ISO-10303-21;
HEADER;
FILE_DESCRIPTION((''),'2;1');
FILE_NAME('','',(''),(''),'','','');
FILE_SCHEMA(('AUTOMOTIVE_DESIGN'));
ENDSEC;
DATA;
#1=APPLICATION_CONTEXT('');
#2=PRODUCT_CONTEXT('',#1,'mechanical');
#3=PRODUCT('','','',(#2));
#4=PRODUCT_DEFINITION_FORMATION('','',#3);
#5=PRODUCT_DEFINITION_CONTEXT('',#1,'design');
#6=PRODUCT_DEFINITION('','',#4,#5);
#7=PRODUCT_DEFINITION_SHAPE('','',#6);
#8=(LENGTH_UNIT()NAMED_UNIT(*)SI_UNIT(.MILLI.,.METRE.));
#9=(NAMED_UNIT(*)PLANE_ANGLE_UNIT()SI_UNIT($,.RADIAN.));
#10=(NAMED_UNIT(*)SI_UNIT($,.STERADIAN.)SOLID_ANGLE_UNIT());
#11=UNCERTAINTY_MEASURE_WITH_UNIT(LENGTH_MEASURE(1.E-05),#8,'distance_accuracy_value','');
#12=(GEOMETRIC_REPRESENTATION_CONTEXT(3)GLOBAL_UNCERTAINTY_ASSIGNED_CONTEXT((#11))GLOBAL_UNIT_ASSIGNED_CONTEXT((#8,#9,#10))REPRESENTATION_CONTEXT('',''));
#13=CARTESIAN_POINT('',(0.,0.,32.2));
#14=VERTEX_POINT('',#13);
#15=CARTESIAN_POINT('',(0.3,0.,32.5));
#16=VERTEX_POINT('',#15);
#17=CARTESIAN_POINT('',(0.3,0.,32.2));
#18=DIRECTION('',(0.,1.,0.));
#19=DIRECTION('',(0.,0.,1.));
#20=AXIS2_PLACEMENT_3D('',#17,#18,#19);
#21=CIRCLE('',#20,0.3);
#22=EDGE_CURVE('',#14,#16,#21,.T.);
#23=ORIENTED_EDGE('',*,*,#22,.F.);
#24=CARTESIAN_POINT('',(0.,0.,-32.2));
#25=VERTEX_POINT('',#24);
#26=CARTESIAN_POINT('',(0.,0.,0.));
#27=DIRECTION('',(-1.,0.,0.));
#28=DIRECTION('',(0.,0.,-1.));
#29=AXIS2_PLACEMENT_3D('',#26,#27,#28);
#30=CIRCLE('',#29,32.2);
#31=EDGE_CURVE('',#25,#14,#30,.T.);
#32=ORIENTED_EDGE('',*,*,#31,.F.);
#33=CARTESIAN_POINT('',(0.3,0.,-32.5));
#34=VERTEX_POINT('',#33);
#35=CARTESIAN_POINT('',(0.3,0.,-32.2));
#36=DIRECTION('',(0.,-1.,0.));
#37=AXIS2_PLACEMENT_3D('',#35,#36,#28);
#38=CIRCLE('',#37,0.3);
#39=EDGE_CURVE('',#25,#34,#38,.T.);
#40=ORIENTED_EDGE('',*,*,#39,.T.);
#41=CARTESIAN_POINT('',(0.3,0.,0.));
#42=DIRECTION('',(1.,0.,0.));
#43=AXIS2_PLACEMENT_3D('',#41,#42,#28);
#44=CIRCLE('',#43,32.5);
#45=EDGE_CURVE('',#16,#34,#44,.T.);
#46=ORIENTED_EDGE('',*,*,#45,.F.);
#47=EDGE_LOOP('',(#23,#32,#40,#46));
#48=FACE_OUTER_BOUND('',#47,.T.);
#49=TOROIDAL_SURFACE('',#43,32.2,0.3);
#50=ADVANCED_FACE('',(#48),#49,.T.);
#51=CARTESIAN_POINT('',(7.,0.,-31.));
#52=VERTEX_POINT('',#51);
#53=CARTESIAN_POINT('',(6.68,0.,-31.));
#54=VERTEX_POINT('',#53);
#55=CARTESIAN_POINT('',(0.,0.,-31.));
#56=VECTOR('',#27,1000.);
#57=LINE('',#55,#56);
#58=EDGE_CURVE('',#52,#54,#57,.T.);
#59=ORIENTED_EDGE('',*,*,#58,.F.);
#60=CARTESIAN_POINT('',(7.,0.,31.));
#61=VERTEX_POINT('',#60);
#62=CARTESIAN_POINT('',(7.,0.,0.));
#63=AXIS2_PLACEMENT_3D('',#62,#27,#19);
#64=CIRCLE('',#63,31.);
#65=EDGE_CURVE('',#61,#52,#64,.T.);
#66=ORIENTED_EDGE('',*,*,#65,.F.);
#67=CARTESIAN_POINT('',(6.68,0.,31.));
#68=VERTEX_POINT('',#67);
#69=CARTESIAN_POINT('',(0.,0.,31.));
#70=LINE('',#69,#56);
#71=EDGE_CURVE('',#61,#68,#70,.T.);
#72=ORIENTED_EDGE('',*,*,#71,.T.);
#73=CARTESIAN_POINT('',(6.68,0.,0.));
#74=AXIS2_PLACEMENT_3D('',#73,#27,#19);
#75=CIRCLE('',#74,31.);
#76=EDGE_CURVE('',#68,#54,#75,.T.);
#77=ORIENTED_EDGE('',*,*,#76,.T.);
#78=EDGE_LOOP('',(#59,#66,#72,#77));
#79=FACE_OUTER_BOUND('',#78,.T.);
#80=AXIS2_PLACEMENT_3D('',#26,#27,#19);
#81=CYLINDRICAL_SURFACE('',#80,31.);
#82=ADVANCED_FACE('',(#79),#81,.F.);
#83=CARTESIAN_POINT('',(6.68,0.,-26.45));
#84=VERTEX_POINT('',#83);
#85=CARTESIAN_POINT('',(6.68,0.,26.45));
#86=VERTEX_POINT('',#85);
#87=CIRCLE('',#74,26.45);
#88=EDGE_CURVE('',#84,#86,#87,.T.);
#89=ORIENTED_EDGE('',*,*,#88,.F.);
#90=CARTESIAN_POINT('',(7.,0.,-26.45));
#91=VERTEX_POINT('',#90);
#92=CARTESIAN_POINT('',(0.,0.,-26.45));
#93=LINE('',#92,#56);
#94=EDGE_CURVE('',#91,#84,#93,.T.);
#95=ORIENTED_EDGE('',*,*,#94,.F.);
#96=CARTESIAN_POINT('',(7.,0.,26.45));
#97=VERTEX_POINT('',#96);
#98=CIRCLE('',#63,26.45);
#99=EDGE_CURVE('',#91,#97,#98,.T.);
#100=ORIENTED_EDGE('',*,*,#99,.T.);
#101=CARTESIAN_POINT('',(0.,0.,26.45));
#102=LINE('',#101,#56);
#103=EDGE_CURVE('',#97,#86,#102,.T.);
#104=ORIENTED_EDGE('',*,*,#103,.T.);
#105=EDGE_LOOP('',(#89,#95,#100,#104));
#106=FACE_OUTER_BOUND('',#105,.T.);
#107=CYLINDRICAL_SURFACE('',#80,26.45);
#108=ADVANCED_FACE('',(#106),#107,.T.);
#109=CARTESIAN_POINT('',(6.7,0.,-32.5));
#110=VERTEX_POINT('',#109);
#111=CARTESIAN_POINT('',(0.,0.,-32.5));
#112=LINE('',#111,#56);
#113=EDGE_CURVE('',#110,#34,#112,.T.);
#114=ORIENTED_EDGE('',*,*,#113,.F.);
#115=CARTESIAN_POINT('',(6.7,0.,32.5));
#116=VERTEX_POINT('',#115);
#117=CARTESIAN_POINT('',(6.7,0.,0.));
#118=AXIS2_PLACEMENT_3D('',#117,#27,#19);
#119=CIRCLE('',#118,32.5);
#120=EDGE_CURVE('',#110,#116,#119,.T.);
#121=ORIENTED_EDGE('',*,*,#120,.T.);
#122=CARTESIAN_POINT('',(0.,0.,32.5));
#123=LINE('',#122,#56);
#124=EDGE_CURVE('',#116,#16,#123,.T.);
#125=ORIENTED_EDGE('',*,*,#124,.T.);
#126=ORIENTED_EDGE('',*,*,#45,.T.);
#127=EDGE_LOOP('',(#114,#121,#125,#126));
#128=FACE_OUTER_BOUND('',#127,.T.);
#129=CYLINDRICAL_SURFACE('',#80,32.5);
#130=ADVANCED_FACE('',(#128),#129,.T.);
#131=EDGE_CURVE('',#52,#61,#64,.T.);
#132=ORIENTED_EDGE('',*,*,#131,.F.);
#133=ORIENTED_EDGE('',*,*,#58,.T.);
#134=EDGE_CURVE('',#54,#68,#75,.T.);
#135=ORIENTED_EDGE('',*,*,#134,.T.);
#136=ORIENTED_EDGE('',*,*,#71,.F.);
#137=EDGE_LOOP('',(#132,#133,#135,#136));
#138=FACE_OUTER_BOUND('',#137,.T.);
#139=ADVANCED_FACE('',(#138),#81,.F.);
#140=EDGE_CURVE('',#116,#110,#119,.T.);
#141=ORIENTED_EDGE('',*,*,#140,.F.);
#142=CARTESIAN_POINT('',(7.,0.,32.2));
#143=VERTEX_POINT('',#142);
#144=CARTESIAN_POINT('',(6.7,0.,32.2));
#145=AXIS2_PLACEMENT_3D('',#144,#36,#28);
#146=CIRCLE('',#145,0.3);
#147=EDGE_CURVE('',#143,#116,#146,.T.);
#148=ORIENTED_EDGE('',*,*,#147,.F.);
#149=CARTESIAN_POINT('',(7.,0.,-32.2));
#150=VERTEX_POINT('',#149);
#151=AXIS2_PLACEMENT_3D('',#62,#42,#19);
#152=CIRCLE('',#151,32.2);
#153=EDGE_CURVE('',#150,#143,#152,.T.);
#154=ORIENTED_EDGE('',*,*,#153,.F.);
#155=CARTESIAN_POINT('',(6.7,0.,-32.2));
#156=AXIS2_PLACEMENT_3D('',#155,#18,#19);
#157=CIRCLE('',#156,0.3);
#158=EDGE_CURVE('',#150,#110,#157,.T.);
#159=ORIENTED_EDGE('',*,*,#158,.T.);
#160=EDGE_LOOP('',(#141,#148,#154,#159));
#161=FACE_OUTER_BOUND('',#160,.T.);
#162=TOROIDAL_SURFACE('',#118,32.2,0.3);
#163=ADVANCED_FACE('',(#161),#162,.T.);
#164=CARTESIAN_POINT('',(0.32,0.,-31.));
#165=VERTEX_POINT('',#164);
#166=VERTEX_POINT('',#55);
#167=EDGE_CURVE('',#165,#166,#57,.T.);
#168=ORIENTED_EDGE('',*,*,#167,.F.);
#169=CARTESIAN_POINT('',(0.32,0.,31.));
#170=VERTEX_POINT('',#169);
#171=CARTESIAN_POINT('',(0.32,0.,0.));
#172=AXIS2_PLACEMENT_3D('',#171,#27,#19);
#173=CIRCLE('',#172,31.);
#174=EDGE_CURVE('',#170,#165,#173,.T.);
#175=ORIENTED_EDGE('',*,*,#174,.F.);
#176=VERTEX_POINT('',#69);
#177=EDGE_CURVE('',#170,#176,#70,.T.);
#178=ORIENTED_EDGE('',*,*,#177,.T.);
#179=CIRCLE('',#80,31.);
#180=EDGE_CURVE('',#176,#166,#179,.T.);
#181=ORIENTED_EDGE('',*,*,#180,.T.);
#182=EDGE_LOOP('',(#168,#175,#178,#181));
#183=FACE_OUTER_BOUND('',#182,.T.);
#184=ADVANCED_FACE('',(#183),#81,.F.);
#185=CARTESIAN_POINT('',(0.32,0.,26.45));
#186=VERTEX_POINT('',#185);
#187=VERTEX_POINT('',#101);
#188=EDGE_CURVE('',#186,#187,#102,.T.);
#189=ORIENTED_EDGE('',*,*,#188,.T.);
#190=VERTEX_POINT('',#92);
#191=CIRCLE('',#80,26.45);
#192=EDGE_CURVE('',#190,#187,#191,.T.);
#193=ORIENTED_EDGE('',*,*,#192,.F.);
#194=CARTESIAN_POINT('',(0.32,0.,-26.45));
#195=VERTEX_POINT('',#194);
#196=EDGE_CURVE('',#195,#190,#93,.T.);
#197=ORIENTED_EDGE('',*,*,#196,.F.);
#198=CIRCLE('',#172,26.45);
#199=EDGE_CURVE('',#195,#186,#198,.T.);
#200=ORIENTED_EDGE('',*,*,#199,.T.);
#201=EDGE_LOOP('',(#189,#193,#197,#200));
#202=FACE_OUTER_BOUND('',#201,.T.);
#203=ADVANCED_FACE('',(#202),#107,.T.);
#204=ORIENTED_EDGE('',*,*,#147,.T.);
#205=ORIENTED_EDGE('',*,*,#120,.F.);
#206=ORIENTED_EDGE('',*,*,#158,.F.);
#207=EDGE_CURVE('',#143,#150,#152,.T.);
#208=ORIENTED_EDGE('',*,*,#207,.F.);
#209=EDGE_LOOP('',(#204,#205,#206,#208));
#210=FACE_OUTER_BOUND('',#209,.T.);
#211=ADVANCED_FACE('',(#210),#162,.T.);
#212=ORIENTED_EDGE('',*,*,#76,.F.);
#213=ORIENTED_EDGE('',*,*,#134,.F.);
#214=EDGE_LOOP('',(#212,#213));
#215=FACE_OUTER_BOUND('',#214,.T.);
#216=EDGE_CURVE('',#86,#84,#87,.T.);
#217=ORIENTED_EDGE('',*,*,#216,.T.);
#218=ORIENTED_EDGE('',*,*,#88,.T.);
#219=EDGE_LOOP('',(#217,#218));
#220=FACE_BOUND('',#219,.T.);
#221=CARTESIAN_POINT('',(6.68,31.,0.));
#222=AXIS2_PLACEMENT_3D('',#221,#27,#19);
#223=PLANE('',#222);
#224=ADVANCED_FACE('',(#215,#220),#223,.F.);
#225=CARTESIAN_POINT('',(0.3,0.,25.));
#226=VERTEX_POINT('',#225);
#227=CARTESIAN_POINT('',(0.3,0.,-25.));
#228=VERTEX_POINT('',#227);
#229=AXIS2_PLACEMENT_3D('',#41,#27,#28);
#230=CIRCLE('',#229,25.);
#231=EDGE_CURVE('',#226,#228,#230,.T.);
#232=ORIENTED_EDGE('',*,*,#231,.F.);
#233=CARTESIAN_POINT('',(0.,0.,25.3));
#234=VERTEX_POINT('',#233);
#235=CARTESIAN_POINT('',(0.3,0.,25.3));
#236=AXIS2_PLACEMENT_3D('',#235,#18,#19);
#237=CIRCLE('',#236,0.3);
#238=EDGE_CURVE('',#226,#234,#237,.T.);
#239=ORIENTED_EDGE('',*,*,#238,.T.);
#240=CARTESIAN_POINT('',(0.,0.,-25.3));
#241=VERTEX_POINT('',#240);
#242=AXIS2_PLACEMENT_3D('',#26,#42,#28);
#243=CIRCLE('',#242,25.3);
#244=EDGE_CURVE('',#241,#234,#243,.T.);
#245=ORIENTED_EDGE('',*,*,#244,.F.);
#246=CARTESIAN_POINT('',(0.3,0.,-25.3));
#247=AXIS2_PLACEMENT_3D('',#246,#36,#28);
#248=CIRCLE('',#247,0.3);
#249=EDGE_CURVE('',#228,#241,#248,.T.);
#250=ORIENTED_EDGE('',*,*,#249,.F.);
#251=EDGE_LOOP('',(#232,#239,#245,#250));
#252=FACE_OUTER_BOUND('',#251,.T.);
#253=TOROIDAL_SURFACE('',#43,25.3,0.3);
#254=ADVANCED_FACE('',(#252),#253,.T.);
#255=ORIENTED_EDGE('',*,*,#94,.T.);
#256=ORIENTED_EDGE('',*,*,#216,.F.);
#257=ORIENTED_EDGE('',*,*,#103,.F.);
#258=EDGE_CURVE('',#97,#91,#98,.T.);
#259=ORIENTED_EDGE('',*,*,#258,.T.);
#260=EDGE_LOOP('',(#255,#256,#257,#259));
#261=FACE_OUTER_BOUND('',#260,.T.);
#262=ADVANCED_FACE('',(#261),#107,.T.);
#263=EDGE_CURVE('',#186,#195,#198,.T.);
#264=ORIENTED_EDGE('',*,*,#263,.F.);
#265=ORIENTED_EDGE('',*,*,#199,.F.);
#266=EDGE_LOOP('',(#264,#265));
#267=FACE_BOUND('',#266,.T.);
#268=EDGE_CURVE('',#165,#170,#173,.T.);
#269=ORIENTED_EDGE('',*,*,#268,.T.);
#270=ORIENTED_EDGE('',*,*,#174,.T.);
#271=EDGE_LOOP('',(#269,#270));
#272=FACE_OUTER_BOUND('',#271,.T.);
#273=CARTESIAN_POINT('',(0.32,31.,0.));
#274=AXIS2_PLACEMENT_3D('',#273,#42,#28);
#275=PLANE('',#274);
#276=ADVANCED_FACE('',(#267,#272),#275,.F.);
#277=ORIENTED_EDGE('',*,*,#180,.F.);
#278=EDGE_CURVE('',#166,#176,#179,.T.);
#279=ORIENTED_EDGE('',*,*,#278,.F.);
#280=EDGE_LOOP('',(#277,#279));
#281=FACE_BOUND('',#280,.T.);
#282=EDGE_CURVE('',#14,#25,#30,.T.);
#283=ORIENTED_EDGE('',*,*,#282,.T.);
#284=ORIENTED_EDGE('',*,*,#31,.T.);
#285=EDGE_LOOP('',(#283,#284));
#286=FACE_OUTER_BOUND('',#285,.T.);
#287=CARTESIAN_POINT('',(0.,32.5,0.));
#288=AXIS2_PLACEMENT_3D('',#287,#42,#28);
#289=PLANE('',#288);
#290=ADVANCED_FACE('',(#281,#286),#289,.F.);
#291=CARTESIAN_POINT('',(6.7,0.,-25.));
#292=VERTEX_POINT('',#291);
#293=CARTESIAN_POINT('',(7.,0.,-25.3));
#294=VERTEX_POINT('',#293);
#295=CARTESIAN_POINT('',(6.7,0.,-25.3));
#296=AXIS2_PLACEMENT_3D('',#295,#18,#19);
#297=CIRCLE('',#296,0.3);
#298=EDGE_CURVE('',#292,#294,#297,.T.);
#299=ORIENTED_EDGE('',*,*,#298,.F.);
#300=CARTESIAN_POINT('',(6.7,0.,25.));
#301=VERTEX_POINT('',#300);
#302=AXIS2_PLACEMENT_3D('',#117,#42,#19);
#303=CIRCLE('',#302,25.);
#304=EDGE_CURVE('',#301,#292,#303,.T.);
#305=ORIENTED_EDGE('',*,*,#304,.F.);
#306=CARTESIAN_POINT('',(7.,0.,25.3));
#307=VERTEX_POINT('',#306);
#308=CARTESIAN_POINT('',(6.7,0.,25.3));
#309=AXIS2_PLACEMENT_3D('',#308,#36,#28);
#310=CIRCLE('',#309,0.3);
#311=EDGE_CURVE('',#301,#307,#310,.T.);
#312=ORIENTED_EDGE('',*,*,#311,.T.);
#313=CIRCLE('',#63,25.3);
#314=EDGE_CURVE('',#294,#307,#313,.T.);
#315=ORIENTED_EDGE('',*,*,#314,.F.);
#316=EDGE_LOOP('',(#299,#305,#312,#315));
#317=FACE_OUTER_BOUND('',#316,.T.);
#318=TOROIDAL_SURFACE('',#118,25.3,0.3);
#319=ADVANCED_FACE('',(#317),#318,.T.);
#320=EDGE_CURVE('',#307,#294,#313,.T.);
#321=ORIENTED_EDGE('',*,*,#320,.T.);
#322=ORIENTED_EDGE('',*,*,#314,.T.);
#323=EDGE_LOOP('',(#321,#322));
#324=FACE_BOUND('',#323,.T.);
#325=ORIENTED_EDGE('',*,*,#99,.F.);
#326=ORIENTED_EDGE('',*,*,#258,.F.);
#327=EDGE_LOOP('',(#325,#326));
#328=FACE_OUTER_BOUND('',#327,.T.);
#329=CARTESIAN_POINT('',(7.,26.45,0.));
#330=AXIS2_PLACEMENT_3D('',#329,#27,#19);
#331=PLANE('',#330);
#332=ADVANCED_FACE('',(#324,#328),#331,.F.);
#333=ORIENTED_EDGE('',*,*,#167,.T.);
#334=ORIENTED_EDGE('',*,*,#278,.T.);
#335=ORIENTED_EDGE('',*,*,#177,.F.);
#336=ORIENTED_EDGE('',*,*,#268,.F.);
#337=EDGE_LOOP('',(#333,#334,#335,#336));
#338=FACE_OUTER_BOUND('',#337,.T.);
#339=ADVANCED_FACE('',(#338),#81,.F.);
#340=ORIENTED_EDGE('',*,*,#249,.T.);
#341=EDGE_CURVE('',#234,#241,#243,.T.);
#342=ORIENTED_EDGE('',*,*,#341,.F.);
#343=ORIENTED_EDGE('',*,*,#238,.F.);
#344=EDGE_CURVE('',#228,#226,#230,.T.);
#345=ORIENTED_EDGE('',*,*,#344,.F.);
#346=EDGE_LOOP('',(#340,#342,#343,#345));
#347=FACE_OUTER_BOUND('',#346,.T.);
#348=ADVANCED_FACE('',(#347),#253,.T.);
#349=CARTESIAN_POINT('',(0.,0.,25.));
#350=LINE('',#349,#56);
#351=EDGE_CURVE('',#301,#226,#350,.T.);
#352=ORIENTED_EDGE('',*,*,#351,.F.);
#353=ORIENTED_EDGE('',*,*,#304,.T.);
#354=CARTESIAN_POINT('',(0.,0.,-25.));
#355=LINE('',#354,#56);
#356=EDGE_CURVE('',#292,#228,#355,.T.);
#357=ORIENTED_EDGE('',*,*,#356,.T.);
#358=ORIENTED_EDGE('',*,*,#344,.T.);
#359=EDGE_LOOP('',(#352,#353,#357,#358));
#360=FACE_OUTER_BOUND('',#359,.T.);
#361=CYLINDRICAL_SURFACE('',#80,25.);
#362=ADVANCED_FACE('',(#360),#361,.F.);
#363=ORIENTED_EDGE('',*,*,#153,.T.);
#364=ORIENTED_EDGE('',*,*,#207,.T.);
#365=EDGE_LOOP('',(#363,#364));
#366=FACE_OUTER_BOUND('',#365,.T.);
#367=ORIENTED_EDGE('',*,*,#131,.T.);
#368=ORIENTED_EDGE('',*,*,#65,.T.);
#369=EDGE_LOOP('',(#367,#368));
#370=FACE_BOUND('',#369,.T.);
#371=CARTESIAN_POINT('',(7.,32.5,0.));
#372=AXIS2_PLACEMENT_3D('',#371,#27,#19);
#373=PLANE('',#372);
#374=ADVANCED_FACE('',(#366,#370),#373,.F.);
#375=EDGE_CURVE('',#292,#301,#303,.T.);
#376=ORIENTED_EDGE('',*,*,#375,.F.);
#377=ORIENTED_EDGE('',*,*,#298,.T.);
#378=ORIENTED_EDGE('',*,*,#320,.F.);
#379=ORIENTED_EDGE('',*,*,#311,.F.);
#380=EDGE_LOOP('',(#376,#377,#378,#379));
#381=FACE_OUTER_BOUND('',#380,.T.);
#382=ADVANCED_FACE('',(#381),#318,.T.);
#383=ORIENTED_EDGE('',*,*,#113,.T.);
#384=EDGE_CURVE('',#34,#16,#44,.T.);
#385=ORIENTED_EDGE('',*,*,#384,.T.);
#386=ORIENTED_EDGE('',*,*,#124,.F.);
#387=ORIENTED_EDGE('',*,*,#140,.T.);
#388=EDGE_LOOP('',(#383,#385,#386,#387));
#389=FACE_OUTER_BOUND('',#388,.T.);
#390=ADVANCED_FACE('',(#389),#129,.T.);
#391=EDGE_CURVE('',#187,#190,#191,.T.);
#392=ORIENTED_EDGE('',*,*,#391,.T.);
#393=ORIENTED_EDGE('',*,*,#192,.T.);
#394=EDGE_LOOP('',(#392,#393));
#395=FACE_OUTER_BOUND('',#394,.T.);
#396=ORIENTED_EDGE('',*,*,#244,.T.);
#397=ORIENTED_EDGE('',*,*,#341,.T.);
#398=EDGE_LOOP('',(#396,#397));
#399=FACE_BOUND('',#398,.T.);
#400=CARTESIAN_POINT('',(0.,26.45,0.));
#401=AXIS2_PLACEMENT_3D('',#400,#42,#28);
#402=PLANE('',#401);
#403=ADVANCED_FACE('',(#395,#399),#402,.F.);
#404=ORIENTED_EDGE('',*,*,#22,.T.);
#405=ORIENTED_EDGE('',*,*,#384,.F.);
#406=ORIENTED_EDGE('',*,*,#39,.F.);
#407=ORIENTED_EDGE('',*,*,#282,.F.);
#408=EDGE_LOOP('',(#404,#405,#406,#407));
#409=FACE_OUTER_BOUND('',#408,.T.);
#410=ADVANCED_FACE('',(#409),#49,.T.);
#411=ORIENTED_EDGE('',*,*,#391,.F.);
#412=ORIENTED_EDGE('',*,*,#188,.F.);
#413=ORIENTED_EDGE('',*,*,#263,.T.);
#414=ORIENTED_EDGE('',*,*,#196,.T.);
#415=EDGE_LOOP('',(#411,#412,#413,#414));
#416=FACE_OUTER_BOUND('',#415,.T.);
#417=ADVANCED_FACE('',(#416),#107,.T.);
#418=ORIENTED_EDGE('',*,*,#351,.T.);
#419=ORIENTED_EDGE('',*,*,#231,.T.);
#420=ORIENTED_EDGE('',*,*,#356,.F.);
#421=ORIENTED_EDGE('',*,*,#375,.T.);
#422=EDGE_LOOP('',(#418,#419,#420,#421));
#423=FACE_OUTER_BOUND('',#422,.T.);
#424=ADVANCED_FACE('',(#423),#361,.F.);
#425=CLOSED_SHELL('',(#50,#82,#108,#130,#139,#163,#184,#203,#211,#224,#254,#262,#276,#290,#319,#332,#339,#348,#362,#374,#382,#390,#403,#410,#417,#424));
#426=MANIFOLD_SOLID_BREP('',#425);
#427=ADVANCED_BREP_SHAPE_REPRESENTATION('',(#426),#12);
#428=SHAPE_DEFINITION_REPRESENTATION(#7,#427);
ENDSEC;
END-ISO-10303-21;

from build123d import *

# Parameters (mm, degrees)
FILLET1_R = 0.3
FILLET2_R = 0.3


with BuildPart() as part:
    # Sketch1 → Revolve1 (revolve)
    with BuildSketch(Plane.XY, mode=Mode.PRIVATE) as revolve1_sk:
        Polygon((0, 25), (7, 25), (7, 26.45), (6.68, 26.45), (6.68, 31), (7, 31), (7, 32.5), (0, 32.5), (0, 31), (0.32, 31), (0.32, 26.45), (0, 26.45), align=None)
    revolve(revolve1_sk.sketch.rotate(Axis((0, 0, 0), (1, 0, 0)), 90), axis=Axis((0, 0, 0), (1, 0, 0)))

    # Fillet1
    fillet1_edges = [part.edges().sort_by_distance(p)[0] for p in [
        (0, 0, -32.5),
        (7, 0, -32.5),
    ]]
    fillet(fillet1_edges, radius=FILLET1_R)

    # Fillet2
    fillet2_edges = [part.edges().sort_by_distance(p)[0] for p in [
        (7, 0, -25),
        (0, 0, -25),
    ]]
    fillet(fillet2_edges, radius=FILLET2_R)


solid = part.part
